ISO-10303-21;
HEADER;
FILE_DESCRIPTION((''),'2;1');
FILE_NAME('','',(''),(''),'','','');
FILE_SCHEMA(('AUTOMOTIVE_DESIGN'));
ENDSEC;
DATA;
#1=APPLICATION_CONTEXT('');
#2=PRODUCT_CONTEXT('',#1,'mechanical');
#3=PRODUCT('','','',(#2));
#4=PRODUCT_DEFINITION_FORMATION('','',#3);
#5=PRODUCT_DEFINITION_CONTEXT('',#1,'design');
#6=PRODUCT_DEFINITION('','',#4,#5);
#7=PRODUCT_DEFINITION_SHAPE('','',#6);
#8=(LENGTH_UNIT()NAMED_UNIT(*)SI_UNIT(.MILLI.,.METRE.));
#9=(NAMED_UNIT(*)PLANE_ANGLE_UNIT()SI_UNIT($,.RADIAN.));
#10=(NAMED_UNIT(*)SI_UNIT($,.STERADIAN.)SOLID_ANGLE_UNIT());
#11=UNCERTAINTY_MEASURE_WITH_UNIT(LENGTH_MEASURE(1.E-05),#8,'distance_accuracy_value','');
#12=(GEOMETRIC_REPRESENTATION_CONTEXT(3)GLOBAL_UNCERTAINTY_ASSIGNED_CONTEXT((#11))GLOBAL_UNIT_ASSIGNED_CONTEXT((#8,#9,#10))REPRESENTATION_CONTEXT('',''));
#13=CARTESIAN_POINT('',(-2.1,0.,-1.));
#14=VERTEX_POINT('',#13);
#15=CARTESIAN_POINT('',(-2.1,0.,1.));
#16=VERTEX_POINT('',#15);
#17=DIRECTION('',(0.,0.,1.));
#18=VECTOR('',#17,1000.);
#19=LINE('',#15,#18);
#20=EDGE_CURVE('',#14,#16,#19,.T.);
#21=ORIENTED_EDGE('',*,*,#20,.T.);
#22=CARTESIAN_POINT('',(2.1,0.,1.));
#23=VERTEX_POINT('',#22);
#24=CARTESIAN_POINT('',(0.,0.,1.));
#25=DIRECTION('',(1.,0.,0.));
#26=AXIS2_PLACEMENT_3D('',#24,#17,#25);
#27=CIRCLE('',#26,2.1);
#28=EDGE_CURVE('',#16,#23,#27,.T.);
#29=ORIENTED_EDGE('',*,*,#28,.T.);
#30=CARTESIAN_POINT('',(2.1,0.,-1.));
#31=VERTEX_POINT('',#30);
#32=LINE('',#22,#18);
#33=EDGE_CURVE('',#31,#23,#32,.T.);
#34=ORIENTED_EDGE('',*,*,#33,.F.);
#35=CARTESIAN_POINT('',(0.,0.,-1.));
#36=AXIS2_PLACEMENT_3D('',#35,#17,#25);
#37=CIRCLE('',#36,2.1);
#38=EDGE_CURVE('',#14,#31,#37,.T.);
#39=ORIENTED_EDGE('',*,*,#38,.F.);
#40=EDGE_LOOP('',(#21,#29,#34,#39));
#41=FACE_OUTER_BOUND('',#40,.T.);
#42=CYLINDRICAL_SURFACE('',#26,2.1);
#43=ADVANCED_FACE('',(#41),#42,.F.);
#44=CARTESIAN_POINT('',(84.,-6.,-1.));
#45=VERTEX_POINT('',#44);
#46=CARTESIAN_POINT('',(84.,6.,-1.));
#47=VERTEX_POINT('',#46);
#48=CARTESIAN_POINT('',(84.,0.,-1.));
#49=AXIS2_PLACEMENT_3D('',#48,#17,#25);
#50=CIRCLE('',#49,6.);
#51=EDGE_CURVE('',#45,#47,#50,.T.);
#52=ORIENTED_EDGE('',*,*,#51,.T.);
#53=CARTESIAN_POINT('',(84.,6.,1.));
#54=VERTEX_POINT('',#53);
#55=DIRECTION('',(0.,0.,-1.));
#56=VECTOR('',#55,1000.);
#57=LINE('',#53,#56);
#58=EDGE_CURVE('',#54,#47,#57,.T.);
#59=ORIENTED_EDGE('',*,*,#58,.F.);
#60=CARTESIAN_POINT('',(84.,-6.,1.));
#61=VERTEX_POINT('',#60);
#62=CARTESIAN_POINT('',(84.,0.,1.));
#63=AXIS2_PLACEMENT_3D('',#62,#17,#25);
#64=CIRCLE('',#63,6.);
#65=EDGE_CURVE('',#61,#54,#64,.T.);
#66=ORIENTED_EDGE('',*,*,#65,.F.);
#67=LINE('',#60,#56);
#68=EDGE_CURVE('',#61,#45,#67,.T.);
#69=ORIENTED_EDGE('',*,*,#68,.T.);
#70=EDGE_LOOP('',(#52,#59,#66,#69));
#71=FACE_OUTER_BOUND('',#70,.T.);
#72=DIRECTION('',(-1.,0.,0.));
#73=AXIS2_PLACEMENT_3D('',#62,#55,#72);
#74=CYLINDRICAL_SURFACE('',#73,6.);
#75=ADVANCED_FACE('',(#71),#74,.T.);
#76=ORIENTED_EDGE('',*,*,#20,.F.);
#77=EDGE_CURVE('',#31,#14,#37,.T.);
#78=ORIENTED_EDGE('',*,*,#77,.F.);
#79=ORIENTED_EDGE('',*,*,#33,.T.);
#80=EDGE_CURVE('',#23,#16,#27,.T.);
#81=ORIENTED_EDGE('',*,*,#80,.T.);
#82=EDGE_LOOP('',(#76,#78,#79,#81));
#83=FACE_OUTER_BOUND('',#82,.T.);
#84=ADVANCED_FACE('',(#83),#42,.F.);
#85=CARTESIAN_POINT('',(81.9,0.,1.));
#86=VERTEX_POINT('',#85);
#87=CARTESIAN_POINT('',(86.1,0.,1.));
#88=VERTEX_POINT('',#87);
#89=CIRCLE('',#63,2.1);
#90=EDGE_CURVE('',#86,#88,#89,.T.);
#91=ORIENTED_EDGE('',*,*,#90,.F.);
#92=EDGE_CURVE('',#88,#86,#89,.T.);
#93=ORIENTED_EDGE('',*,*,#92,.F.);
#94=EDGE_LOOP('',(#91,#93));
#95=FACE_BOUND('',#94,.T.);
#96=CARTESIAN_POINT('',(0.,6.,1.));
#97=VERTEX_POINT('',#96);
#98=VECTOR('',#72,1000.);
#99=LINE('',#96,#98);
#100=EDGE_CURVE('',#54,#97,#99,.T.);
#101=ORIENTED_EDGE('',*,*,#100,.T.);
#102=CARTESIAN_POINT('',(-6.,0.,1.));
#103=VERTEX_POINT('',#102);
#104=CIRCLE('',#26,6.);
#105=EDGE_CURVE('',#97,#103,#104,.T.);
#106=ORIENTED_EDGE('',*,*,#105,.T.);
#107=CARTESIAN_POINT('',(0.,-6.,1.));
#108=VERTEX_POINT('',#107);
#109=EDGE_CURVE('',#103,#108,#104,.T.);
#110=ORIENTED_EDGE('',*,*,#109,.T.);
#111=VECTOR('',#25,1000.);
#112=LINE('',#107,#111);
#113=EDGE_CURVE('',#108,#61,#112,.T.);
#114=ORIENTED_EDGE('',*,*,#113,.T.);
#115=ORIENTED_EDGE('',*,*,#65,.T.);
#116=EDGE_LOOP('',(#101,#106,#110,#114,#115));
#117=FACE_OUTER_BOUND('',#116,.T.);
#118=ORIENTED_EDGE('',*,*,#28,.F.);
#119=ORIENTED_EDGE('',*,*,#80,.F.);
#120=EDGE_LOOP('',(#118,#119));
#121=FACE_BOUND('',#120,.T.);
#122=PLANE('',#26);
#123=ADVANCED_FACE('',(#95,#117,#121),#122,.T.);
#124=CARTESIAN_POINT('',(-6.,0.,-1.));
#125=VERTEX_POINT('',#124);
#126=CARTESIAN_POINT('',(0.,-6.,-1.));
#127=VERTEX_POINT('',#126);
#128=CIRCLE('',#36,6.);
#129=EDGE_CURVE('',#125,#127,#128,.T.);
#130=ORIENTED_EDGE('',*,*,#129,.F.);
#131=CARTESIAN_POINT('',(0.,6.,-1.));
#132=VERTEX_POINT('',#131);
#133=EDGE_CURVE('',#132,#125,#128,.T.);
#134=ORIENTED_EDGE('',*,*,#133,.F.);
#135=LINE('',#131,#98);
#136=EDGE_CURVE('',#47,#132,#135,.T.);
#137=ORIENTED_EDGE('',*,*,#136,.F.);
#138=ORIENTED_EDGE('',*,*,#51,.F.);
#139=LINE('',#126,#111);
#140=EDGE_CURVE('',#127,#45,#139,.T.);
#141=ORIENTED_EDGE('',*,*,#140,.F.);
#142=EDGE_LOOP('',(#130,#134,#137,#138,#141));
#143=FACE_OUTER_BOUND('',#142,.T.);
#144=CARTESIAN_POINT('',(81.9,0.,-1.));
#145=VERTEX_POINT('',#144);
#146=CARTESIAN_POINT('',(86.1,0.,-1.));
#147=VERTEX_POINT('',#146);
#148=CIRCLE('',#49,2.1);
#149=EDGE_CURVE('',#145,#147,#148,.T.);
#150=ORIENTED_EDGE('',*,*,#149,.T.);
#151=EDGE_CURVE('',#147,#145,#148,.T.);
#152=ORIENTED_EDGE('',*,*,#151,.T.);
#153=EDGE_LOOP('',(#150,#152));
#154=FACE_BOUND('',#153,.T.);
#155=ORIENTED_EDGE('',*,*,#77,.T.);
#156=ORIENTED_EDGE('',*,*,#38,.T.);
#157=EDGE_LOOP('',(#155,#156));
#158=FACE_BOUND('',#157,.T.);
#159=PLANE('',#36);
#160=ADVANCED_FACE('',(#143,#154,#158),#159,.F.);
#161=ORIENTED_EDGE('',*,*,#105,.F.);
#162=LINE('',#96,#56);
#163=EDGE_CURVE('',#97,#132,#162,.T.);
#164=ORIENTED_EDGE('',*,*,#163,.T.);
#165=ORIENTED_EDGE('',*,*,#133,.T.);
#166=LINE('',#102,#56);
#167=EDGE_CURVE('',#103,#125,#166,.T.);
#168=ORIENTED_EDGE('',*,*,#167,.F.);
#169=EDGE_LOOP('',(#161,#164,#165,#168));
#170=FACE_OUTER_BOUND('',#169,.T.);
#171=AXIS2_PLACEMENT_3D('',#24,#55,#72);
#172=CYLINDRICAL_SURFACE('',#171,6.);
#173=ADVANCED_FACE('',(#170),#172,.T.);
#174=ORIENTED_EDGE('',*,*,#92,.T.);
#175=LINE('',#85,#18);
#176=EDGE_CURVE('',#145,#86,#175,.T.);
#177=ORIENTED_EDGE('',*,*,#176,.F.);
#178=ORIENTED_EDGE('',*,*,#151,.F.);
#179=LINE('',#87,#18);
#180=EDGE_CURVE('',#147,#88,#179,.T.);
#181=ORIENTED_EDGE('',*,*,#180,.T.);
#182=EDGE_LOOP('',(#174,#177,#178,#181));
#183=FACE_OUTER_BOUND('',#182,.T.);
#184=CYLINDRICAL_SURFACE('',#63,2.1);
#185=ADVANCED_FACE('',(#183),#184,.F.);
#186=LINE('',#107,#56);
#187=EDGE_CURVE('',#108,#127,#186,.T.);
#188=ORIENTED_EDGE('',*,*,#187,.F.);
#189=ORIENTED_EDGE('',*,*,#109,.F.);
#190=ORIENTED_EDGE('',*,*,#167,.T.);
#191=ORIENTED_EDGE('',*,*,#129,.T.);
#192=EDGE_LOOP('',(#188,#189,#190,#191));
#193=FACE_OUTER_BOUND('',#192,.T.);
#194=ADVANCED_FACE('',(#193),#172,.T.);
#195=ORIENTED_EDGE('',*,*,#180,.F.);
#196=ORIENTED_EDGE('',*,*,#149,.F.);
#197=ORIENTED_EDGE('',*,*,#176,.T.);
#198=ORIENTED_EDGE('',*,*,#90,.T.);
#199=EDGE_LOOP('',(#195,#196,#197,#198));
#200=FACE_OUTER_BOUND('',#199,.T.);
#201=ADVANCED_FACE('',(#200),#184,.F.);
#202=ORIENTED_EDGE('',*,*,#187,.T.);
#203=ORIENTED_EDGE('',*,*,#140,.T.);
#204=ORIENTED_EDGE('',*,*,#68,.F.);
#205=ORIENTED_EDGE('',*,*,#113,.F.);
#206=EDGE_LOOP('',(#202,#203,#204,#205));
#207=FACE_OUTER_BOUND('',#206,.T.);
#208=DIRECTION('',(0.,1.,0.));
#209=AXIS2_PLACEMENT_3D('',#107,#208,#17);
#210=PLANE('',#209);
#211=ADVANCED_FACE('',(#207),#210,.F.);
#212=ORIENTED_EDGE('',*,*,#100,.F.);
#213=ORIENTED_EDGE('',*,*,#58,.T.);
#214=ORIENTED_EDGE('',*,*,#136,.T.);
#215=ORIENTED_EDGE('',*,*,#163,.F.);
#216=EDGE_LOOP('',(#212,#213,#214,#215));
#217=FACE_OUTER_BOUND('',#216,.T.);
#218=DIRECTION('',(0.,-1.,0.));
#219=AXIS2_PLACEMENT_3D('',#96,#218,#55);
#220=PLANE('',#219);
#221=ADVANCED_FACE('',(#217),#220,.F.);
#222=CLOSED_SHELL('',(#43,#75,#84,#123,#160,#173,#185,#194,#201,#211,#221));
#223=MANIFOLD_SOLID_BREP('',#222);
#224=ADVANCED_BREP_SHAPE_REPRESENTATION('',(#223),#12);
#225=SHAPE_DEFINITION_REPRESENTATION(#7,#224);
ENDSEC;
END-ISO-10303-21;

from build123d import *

# Parameters (mm, degrees)
BOSS_EXTRUDE1_DEPTH        = 1
F_4_2_4_2_DIAMETER_HOLE1_D = 4.2


with BuildPart() as part:
    # Sketch1 → Boss-Extrude1 (new, symmetric)
    with BuildSketch(Plane.XY):
        with BuildLine():
            Line((0, 6), (84, 6))
            ThreePointArc((84, 6), (90, 0), (84, -6))
            Line((84, -6), (0, -6))
            ThreePointArc((0, -6), (-6, 0), (0, 6))
        make_face()
    extrude(amount=BOSS_EXTRUDE1_DEPTH, both=True)

    # Ø4.2 (4.2) Diameter Hole1 (through all)
    with Locations(Plane.XY.offset(1)):
        with Locations((0, 0), (84, 0)):
            Hole(F_4_2_4_2_DIAMETER_HOLE1_D / 2)


solid = part.part
